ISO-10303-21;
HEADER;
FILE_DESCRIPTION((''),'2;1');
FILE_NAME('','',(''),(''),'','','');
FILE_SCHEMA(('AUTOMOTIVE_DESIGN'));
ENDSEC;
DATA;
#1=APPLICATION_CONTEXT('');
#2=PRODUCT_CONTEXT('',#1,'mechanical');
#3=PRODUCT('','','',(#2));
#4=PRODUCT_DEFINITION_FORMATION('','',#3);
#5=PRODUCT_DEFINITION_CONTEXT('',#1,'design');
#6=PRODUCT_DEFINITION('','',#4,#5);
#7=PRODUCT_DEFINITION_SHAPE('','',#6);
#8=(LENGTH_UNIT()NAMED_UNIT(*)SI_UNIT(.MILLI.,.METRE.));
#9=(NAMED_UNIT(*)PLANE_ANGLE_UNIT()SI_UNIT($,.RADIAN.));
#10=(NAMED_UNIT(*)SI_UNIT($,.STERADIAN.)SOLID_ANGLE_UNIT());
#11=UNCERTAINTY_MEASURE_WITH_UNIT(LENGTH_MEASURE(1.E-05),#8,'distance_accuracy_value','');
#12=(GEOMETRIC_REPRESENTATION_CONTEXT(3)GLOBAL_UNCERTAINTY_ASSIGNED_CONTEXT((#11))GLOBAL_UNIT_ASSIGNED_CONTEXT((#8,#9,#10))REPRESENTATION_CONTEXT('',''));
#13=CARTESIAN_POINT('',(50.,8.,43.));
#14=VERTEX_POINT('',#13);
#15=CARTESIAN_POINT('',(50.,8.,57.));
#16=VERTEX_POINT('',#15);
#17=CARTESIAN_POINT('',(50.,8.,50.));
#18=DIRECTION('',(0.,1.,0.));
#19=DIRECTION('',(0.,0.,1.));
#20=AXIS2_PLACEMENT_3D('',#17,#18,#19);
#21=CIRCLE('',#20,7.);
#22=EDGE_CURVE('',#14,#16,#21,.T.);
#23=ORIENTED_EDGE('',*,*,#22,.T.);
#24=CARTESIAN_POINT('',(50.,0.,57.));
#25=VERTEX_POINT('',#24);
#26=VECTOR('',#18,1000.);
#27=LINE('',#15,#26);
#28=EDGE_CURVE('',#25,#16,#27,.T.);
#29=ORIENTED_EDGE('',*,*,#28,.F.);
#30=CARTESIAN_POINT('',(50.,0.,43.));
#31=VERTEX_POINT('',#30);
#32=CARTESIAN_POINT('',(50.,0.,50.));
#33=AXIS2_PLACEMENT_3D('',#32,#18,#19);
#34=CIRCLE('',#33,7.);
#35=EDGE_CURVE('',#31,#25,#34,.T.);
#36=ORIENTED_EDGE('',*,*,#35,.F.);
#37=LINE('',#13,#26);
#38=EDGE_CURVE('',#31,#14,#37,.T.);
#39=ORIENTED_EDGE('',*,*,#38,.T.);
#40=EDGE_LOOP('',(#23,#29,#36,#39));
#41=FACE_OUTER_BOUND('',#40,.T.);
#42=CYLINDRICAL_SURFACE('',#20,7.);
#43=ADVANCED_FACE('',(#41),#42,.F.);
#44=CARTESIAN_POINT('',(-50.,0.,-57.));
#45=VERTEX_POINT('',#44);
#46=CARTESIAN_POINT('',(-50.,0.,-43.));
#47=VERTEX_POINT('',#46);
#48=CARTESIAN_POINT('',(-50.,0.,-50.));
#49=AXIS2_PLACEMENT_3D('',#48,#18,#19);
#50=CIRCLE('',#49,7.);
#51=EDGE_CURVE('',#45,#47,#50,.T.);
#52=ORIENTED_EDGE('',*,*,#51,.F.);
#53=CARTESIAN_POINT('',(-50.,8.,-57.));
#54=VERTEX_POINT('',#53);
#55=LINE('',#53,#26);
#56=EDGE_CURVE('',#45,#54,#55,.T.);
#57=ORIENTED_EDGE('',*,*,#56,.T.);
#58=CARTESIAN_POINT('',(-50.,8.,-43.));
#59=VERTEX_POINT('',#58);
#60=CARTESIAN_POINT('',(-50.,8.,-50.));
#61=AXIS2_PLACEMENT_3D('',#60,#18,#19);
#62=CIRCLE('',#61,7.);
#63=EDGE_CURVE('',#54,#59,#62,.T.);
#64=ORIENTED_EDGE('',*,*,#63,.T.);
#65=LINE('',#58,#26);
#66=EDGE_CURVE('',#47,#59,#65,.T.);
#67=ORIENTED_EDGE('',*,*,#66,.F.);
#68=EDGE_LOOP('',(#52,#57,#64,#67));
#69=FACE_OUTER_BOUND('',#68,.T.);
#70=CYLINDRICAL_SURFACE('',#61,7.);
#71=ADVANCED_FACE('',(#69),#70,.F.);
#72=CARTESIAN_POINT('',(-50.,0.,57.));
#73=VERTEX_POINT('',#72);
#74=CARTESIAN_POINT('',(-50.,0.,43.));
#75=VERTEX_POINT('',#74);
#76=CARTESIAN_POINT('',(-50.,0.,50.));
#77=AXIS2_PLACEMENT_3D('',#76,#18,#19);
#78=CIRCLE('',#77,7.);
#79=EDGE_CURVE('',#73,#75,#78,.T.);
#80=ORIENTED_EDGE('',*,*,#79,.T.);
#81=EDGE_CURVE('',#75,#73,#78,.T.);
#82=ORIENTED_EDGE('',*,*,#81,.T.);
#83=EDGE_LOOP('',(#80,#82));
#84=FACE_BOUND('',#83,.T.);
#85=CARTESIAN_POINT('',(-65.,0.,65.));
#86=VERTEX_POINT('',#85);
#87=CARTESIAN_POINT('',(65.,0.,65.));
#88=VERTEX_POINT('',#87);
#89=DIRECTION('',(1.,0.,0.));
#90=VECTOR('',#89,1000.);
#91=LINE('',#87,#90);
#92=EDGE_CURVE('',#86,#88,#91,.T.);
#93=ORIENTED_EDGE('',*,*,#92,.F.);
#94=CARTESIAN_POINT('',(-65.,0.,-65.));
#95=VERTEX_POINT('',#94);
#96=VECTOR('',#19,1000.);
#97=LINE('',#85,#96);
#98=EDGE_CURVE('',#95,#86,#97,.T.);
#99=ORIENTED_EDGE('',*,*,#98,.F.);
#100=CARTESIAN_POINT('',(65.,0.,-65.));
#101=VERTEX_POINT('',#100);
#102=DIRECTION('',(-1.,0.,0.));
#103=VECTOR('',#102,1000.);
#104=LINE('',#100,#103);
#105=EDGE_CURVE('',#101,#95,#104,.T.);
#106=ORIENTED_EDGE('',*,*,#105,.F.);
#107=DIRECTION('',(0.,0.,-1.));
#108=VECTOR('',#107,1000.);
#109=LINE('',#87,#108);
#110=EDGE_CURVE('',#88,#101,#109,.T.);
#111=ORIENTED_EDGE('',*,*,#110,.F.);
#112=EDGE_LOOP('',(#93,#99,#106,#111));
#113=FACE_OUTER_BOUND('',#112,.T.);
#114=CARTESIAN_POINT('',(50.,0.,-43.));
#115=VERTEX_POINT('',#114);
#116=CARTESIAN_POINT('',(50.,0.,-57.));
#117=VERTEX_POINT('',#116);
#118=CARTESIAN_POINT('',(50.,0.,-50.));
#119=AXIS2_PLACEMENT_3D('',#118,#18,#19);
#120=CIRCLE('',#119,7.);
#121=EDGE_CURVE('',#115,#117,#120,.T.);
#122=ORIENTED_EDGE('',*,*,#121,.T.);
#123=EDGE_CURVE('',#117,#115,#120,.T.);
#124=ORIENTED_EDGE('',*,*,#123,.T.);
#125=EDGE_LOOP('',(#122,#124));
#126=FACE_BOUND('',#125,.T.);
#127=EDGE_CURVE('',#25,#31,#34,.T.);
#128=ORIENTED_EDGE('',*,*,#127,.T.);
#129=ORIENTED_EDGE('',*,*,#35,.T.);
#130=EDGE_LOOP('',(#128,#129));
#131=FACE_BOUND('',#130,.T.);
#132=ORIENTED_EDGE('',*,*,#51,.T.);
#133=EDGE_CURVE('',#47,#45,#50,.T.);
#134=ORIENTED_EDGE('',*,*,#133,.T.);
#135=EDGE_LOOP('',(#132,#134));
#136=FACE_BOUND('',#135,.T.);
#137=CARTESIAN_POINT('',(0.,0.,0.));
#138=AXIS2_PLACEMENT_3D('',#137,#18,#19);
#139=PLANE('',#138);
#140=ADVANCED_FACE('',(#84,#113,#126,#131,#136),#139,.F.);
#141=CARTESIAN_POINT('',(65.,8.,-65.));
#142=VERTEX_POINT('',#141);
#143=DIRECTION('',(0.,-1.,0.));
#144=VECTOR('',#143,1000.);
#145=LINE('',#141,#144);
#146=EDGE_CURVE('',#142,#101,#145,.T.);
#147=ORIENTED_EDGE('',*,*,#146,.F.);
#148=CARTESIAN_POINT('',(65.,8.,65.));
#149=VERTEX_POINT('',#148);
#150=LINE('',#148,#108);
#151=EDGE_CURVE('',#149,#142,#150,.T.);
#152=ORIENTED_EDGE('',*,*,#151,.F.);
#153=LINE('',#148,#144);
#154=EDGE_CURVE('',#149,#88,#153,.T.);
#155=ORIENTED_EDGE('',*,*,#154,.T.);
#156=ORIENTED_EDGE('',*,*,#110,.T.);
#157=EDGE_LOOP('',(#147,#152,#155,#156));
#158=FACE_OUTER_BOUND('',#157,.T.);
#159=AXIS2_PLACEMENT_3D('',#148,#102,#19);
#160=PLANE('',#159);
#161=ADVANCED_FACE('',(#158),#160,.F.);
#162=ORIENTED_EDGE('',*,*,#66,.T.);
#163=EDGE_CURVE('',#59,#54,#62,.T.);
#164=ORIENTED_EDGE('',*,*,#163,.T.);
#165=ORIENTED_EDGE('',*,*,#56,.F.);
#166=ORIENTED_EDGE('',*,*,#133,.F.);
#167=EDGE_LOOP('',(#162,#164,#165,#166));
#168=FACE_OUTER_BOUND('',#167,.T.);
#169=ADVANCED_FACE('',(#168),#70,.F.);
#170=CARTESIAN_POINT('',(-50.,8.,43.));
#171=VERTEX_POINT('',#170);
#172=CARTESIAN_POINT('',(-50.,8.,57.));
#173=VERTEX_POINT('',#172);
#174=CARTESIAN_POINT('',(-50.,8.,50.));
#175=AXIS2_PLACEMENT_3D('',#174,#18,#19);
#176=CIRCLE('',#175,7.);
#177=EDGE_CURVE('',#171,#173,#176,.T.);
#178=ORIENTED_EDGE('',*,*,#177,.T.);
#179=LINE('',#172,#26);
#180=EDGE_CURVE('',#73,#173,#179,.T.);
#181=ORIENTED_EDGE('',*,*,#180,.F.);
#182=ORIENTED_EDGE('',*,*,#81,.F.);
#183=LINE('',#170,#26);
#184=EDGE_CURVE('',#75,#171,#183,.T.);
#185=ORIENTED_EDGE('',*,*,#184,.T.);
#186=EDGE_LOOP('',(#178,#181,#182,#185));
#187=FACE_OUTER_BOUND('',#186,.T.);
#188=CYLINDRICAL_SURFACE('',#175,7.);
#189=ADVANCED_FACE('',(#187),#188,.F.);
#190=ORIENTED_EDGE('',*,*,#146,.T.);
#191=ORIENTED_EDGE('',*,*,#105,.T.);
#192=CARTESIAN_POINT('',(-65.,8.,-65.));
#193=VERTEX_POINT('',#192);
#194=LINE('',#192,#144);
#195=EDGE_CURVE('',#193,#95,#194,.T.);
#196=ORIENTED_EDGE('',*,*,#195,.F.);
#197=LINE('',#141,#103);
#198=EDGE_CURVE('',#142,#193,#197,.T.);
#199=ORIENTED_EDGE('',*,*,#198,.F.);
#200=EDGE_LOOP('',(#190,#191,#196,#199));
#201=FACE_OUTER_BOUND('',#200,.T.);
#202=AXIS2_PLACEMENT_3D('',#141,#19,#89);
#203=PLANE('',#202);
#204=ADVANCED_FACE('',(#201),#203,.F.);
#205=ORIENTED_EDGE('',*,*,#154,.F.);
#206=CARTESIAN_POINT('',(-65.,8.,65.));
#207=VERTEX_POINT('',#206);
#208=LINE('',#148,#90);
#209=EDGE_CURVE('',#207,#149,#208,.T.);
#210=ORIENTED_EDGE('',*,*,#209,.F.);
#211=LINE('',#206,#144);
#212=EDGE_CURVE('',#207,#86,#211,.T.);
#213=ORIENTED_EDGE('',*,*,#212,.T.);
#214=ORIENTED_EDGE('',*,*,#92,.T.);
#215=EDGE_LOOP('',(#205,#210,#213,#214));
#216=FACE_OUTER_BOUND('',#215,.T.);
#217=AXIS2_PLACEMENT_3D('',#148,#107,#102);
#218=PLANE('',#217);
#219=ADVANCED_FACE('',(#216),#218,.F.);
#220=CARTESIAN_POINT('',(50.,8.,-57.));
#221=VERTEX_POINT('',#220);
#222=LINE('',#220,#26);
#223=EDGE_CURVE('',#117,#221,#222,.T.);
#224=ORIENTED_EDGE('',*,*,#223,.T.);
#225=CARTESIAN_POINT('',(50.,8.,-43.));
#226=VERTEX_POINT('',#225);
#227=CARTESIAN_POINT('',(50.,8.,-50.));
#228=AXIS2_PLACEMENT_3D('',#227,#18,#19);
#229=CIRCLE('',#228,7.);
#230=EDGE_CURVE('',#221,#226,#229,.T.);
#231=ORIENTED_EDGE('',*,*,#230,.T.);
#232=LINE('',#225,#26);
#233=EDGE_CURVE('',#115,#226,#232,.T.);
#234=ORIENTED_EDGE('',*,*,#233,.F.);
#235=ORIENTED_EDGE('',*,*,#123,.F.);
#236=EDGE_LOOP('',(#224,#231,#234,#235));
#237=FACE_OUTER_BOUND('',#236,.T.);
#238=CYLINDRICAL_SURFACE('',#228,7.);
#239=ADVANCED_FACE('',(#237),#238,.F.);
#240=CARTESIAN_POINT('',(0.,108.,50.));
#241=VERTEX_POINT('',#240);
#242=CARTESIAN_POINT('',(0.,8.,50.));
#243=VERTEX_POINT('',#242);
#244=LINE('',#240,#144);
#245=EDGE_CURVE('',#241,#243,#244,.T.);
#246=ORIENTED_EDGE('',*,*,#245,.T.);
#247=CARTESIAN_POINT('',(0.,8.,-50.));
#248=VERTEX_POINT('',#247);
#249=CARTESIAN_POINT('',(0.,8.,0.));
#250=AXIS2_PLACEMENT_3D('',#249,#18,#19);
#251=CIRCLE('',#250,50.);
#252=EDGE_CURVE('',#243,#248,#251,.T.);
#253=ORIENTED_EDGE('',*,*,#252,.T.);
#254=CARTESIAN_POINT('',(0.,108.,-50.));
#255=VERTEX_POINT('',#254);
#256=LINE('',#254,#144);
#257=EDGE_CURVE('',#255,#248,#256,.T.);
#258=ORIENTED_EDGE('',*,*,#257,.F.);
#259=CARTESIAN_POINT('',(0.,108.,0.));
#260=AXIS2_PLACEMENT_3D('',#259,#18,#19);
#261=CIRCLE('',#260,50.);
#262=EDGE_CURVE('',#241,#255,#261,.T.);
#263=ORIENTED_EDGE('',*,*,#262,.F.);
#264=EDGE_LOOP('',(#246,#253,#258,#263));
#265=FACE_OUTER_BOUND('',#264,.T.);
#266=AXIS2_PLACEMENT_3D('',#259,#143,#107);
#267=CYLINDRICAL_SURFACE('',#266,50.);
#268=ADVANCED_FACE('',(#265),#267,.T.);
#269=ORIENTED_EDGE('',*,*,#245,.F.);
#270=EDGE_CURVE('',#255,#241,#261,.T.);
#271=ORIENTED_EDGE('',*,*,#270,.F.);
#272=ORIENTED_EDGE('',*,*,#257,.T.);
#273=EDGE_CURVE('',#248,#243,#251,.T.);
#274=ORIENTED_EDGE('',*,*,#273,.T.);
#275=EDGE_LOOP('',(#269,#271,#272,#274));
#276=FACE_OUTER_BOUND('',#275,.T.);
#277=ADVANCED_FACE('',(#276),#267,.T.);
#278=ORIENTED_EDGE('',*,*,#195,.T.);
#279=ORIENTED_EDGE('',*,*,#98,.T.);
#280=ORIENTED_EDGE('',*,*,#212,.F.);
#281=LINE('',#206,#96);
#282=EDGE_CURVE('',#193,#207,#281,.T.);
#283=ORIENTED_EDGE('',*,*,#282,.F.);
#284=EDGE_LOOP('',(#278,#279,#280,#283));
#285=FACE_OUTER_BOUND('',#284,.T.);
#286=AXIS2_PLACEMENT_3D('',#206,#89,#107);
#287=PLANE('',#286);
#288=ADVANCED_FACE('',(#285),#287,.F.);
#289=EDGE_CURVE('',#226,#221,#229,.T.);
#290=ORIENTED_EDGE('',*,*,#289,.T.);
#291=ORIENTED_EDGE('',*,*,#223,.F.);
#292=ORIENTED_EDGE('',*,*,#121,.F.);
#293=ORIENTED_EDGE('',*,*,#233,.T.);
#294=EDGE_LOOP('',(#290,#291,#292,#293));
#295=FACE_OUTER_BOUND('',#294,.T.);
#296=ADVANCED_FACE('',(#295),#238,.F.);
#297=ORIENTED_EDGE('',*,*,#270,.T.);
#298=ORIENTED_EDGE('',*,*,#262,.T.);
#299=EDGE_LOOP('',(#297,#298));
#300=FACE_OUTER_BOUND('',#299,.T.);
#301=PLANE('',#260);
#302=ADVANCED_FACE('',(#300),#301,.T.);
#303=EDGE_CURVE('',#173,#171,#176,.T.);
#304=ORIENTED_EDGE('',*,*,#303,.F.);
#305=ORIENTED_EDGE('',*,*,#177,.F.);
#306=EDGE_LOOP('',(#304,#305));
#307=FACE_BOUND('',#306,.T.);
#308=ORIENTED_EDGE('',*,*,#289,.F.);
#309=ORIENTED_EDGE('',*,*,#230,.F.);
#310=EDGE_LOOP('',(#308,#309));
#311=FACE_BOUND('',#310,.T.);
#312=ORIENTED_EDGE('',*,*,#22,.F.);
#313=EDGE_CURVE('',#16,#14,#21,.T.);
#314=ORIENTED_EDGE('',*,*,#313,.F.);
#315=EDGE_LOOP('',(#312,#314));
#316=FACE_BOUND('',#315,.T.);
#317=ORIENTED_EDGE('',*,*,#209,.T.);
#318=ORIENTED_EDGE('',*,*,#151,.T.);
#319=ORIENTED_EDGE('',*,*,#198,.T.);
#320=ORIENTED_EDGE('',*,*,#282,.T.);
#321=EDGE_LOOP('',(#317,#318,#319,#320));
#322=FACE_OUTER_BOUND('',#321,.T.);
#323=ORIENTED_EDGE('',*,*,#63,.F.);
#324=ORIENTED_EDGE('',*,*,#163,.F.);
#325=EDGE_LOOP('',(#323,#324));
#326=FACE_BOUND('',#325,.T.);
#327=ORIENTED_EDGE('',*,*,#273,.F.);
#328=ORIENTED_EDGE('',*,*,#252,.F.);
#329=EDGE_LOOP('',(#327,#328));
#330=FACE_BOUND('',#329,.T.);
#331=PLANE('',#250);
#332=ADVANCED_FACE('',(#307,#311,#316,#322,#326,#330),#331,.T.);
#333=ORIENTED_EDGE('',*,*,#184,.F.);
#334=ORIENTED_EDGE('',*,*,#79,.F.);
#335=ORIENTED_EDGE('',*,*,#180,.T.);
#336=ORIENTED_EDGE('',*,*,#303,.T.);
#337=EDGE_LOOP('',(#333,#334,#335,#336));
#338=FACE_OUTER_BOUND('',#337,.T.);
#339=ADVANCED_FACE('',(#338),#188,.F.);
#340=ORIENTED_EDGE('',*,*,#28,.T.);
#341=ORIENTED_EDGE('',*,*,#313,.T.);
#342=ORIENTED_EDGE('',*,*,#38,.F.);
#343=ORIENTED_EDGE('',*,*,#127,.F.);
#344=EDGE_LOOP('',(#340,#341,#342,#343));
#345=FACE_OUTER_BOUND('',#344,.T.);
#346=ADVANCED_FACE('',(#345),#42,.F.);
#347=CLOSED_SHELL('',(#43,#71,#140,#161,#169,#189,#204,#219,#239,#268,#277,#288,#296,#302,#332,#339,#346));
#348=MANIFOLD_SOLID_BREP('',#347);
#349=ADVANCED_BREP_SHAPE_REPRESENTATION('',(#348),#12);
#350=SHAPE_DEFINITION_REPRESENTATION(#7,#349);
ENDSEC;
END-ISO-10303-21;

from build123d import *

# Parameters (mm, degrees)
SKETCH1_W                      = 130
SKETCH1_H                      = 130
BOSS_EXTRUDE1_DEPTH            = 8
SKETCH2_R                      = 50
BOSS_EXTRUDE2_DEPTH            = 100
F_14_0_14_DIAMETER_HOLE1_D     = 14
F_14_0_14_DIAMETER_HOLE1_DEPTH = 22
F_14_0_14_DIAMETER_HOLE1_TIP   = 4.206024333


with BuildPart() as part:
    # Sketch1 → Boss-Extrude1 (new body)
    with BuildSketch(Plane(origin=(0, 0, 0), x_dir=(1, 0, 0), z_dir=(0, 1, 0))):
        Rectangle(SKETCH1_W, SKETCH1_H)
    extrude(amount=BOSS_EXTRUDE1_DEPTH)

    # Sketch2 → Boss-Extrude2 (add)
    with BuildSketch(Plane(origin=(0, 8, 0), x_dir=(1, 0, 0), z_dir=(0, 1, 0))):
        with Locations(Location((0, 0, 0), (0, 0, 270))):
            Circle(SKETCH2_R)
    extrude(amount=BOSS_EXTRUDE2_DEPTH)

    # Ø14.0 (14) Diameter Hole1
    with Locations(Plane(origin=(0, 8, 0), x_dir=(1, 0, 0), z_dir=(0, 1, 0))):
        with Locations((-50, 50), (50, 50), (50, -50), (-50, -50)):
            Hole(F_14_0_14_DIAMETER_HOLE1_D / 2, depth=F_14_0_14_DIAMETER_HOLE1_DEPTH)
            with Locations((0, 0, -(F_14_0_14_DIAMETER_HOLE1_DEPTH + F_14_0_14_DIAMETER_HOLE1_TIP / 2))):  # 118° drill point
                Cone(0, F_14_0_14_DIAMETER_HOLE1_D / 2, F_14_0_14_DIAMETER_HOLE1_TIP, mode=Mode.SUBTRACT)


solid = part.part
